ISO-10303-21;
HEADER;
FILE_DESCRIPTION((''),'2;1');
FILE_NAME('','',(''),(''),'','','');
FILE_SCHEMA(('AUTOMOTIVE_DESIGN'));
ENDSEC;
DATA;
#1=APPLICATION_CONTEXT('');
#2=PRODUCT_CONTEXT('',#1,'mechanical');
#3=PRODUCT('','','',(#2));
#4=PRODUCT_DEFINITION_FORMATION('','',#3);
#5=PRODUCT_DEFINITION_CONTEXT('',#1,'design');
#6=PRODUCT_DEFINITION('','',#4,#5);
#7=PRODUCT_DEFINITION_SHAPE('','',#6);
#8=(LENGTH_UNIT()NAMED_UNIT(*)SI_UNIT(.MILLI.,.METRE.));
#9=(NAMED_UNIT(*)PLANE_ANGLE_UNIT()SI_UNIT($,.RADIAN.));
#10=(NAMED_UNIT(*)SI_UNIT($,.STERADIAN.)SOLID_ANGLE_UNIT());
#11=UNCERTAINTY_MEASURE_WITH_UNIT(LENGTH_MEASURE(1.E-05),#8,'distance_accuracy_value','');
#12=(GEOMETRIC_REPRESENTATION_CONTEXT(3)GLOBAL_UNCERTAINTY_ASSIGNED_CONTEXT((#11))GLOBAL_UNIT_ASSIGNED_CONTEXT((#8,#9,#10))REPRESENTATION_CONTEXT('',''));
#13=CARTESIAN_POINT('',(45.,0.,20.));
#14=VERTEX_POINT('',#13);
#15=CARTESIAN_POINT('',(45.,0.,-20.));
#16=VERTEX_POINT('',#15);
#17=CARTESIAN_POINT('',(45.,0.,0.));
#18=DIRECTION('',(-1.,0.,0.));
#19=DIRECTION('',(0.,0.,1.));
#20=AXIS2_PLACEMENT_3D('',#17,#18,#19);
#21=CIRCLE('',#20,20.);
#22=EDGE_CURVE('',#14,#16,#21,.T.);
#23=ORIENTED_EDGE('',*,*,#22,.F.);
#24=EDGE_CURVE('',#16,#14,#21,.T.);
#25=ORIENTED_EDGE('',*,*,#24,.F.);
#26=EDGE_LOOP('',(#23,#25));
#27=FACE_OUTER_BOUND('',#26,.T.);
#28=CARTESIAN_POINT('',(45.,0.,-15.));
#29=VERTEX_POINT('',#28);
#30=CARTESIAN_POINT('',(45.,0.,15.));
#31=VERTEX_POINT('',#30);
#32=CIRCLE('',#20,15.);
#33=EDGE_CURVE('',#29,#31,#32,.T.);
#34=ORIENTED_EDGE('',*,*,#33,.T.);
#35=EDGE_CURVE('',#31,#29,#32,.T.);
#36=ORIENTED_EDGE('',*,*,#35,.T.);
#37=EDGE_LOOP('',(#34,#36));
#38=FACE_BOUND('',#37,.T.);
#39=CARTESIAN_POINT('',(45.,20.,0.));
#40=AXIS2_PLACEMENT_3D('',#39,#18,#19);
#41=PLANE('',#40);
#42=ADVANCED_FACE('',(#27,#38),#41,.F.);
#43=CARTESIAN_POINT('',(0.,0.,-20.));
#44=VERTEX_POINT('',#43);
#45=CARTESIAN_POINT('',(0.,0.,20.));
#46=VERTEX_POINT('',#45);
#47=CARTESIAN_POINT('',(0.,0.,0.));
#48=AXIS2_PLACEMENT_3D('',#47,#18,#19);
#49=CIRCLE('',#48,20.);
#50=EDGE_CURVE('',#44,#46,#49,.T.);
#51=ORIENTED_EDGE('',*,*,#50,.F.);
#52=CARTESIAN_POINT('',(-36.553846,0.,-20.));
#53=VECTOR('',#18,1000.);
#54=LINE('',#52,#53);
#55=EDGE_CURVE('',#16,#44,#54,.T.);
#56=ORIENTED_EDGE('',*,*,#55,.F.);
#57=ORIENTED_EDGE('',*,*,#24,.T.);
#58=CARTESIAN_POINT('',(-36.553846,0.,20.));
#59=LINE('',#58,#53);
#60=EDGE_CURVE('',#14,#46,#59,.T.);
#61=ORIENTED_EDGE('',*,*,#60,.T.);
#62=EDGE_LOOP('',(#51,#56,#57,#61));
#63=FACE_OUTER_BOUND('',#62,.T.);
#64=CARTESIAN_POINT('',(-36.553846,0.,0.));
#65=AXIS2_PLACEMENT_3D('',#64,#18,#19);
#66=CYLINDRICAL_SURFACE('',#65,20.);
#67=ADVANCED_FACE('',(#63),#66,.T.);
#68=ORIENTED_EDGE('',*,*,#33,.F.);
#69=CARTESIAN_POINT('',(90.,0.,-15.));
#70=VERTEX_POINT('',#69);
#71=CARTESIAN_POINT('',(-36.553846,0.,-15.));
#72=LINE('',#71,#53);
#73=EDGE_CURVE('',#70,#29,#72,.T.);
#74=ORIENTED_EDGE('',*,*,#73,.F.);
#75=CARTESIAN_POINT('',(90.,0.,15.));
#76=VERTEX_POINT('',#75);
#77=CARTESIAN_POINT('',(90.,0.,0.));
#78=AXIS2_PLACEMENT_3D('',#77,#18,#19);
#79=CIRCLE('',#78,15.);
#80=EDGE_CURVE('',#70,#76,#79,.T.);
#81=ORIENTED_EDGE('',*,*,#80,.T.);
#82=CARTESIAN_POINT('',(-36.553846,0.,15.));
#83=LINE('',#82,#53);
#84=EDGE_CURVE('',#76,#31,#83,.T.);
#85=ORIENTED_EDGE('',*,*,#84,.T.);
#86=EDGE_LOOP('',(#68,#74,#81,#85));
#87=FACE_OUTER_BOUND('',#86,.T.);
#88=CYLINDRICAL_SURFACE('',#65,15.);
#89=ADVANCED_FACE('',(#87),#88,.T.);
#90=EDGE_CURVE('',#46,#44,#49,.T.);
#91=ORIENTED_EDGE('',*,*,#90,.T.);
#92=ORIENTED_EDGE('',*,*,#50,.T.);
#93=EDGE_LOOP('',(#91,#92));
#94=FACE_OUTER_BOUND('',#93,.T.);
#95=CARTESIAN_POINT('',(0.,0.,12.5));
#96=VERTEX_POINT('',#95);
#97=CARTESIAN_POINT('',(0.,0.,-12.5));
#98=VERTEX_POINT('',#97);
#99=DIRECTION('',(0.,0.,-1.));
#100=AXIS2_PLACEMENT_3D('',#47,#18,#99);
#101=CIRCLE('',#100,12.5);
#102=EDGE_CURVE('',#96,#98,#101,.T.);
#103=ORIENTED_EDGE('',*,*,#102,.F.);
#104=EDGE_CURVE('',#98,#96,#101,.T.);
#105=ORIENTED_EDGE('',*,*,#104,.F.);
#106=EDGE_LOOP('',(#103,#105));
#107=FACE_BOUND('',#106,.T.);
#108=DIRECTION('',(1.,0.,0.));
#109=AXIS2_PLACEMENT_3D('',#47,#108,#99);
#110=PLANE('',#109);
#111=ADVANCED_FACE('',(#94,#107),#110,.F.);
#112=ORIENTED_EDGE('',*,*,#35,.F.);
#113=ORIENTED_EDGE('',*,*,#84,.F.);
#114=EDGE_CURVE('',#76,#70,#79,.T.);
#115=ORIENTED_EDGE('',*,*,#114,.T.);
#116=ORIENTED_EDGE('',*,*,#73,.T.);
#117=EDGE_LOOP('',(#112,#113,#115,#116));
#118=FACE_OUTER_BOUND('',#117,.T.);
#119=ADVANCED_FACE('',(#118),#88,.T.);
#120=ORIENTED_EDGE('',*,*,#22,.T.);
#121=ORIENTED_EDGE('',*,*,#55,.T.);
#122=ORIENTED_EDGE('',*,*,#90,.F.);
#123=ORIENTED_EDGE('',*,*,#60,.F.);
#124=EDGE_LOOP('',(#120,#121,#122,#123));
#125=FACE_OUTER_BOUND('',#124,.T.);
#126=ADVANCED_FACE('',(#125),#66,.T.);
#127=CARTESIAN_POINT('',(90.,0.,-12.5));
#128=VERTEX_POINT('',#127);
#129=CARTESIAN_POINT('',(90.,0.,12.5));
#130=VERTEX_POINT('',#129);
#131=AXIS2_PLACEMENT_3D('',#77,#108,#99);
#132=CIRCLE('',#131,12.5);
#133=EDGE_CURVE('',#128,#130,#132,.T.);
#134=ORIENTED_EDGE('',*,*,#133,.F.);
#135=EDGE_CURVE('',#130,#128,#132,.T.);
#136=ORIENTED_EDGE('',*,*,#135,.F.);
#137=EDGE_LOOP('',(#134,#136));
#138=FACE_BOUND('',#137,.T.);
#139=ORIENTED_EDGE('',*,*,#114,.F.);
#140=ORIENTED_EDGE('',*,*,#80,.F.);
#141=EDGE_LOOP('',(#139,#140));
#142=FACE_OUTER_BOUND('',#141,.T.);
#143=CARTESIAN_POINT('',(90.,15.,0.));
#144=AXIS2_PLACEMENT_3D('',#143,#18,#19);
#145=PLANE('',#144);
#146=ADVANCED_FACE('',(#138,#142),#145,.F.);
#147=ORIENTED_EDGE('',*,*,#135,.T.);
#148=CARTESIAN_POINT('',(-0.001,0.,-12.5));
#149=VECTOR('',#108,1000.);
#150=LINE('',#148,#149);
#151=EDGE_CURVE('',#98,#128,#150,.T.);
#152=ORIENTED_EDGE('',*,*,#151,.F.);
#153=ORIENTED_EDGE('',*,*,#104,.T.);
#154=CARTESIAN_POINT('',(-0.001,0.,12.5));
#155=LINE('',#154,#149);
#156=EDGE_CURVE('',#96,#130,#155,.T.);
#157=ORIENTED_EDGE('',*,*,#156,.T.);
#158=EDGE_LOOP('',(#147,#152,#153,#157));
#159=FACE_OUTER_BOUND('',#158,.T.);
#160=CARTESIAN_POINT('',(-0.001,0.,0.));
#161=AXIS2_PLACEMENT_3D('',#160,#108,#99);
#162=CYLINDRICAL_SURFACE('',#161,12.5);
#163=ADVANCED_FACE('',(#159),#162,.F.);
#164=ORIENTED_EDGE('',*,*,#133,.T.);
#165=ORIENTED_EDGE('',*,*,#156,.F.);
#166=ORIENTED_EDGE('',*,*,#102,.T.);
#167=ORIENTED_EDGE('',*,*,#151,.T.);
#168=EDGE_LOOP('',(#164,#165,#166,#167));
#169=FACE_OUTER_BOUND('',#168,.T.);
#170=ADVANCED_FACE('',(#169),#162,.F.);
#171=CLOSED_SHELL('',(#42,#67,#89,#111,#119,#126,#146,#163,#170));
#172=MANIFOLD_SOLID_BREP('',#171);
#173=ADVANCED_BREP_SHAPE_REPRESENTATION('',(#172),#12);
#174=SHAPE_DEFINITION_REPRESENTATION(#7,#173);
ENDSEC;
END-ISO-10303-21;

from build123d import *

# Parameters (mm, degrees)
CUT_EXTRUDE_1_REACH = 96.34
SKETCH_2_R          = 12.5


with BuildPart() as part:
    # 草图1 → 旋转1 (revolve)
    with BuildSketch(Plane.XY, mode=Mode.PRIVATE) as revolve_1_sk:
        Polygon((0, 0), (0, 20), (45, 20), (45, 15), (90, 15), (90, 0), align=None)
    revolve(revolve_1_sk.sketch.rotate(Axis((-36.553846154, 0, 0), (1, 0, 0)), 90), axis=Axis((-36.553846154, 0, 0), (1, 0, 0)))

    # 草图2 → 切除-拉伸1 (cut, up to next)
    with BuildSketch(Plane(origin=(90, 0, 0), x_dir=(0, 0, -1), z_dir=(1, 0, 0)), mode=Mode.PRIVATE) as cut_extrude_1_sk1:
        Circle(SKETCH_2_R)
    cut_extrude_1_tool1 = extrude(cut_extrude_1_sk1.sketch, amount=-CUT_EXTRUDE_1_REACH, mode=Mode.PRIVATE) & part.part
    add(cut_extrude_1_tool1.solids().sort_by_distance((90, 0, 0))[0], mode=Mode.SUBTRACT)


solid = part.part
